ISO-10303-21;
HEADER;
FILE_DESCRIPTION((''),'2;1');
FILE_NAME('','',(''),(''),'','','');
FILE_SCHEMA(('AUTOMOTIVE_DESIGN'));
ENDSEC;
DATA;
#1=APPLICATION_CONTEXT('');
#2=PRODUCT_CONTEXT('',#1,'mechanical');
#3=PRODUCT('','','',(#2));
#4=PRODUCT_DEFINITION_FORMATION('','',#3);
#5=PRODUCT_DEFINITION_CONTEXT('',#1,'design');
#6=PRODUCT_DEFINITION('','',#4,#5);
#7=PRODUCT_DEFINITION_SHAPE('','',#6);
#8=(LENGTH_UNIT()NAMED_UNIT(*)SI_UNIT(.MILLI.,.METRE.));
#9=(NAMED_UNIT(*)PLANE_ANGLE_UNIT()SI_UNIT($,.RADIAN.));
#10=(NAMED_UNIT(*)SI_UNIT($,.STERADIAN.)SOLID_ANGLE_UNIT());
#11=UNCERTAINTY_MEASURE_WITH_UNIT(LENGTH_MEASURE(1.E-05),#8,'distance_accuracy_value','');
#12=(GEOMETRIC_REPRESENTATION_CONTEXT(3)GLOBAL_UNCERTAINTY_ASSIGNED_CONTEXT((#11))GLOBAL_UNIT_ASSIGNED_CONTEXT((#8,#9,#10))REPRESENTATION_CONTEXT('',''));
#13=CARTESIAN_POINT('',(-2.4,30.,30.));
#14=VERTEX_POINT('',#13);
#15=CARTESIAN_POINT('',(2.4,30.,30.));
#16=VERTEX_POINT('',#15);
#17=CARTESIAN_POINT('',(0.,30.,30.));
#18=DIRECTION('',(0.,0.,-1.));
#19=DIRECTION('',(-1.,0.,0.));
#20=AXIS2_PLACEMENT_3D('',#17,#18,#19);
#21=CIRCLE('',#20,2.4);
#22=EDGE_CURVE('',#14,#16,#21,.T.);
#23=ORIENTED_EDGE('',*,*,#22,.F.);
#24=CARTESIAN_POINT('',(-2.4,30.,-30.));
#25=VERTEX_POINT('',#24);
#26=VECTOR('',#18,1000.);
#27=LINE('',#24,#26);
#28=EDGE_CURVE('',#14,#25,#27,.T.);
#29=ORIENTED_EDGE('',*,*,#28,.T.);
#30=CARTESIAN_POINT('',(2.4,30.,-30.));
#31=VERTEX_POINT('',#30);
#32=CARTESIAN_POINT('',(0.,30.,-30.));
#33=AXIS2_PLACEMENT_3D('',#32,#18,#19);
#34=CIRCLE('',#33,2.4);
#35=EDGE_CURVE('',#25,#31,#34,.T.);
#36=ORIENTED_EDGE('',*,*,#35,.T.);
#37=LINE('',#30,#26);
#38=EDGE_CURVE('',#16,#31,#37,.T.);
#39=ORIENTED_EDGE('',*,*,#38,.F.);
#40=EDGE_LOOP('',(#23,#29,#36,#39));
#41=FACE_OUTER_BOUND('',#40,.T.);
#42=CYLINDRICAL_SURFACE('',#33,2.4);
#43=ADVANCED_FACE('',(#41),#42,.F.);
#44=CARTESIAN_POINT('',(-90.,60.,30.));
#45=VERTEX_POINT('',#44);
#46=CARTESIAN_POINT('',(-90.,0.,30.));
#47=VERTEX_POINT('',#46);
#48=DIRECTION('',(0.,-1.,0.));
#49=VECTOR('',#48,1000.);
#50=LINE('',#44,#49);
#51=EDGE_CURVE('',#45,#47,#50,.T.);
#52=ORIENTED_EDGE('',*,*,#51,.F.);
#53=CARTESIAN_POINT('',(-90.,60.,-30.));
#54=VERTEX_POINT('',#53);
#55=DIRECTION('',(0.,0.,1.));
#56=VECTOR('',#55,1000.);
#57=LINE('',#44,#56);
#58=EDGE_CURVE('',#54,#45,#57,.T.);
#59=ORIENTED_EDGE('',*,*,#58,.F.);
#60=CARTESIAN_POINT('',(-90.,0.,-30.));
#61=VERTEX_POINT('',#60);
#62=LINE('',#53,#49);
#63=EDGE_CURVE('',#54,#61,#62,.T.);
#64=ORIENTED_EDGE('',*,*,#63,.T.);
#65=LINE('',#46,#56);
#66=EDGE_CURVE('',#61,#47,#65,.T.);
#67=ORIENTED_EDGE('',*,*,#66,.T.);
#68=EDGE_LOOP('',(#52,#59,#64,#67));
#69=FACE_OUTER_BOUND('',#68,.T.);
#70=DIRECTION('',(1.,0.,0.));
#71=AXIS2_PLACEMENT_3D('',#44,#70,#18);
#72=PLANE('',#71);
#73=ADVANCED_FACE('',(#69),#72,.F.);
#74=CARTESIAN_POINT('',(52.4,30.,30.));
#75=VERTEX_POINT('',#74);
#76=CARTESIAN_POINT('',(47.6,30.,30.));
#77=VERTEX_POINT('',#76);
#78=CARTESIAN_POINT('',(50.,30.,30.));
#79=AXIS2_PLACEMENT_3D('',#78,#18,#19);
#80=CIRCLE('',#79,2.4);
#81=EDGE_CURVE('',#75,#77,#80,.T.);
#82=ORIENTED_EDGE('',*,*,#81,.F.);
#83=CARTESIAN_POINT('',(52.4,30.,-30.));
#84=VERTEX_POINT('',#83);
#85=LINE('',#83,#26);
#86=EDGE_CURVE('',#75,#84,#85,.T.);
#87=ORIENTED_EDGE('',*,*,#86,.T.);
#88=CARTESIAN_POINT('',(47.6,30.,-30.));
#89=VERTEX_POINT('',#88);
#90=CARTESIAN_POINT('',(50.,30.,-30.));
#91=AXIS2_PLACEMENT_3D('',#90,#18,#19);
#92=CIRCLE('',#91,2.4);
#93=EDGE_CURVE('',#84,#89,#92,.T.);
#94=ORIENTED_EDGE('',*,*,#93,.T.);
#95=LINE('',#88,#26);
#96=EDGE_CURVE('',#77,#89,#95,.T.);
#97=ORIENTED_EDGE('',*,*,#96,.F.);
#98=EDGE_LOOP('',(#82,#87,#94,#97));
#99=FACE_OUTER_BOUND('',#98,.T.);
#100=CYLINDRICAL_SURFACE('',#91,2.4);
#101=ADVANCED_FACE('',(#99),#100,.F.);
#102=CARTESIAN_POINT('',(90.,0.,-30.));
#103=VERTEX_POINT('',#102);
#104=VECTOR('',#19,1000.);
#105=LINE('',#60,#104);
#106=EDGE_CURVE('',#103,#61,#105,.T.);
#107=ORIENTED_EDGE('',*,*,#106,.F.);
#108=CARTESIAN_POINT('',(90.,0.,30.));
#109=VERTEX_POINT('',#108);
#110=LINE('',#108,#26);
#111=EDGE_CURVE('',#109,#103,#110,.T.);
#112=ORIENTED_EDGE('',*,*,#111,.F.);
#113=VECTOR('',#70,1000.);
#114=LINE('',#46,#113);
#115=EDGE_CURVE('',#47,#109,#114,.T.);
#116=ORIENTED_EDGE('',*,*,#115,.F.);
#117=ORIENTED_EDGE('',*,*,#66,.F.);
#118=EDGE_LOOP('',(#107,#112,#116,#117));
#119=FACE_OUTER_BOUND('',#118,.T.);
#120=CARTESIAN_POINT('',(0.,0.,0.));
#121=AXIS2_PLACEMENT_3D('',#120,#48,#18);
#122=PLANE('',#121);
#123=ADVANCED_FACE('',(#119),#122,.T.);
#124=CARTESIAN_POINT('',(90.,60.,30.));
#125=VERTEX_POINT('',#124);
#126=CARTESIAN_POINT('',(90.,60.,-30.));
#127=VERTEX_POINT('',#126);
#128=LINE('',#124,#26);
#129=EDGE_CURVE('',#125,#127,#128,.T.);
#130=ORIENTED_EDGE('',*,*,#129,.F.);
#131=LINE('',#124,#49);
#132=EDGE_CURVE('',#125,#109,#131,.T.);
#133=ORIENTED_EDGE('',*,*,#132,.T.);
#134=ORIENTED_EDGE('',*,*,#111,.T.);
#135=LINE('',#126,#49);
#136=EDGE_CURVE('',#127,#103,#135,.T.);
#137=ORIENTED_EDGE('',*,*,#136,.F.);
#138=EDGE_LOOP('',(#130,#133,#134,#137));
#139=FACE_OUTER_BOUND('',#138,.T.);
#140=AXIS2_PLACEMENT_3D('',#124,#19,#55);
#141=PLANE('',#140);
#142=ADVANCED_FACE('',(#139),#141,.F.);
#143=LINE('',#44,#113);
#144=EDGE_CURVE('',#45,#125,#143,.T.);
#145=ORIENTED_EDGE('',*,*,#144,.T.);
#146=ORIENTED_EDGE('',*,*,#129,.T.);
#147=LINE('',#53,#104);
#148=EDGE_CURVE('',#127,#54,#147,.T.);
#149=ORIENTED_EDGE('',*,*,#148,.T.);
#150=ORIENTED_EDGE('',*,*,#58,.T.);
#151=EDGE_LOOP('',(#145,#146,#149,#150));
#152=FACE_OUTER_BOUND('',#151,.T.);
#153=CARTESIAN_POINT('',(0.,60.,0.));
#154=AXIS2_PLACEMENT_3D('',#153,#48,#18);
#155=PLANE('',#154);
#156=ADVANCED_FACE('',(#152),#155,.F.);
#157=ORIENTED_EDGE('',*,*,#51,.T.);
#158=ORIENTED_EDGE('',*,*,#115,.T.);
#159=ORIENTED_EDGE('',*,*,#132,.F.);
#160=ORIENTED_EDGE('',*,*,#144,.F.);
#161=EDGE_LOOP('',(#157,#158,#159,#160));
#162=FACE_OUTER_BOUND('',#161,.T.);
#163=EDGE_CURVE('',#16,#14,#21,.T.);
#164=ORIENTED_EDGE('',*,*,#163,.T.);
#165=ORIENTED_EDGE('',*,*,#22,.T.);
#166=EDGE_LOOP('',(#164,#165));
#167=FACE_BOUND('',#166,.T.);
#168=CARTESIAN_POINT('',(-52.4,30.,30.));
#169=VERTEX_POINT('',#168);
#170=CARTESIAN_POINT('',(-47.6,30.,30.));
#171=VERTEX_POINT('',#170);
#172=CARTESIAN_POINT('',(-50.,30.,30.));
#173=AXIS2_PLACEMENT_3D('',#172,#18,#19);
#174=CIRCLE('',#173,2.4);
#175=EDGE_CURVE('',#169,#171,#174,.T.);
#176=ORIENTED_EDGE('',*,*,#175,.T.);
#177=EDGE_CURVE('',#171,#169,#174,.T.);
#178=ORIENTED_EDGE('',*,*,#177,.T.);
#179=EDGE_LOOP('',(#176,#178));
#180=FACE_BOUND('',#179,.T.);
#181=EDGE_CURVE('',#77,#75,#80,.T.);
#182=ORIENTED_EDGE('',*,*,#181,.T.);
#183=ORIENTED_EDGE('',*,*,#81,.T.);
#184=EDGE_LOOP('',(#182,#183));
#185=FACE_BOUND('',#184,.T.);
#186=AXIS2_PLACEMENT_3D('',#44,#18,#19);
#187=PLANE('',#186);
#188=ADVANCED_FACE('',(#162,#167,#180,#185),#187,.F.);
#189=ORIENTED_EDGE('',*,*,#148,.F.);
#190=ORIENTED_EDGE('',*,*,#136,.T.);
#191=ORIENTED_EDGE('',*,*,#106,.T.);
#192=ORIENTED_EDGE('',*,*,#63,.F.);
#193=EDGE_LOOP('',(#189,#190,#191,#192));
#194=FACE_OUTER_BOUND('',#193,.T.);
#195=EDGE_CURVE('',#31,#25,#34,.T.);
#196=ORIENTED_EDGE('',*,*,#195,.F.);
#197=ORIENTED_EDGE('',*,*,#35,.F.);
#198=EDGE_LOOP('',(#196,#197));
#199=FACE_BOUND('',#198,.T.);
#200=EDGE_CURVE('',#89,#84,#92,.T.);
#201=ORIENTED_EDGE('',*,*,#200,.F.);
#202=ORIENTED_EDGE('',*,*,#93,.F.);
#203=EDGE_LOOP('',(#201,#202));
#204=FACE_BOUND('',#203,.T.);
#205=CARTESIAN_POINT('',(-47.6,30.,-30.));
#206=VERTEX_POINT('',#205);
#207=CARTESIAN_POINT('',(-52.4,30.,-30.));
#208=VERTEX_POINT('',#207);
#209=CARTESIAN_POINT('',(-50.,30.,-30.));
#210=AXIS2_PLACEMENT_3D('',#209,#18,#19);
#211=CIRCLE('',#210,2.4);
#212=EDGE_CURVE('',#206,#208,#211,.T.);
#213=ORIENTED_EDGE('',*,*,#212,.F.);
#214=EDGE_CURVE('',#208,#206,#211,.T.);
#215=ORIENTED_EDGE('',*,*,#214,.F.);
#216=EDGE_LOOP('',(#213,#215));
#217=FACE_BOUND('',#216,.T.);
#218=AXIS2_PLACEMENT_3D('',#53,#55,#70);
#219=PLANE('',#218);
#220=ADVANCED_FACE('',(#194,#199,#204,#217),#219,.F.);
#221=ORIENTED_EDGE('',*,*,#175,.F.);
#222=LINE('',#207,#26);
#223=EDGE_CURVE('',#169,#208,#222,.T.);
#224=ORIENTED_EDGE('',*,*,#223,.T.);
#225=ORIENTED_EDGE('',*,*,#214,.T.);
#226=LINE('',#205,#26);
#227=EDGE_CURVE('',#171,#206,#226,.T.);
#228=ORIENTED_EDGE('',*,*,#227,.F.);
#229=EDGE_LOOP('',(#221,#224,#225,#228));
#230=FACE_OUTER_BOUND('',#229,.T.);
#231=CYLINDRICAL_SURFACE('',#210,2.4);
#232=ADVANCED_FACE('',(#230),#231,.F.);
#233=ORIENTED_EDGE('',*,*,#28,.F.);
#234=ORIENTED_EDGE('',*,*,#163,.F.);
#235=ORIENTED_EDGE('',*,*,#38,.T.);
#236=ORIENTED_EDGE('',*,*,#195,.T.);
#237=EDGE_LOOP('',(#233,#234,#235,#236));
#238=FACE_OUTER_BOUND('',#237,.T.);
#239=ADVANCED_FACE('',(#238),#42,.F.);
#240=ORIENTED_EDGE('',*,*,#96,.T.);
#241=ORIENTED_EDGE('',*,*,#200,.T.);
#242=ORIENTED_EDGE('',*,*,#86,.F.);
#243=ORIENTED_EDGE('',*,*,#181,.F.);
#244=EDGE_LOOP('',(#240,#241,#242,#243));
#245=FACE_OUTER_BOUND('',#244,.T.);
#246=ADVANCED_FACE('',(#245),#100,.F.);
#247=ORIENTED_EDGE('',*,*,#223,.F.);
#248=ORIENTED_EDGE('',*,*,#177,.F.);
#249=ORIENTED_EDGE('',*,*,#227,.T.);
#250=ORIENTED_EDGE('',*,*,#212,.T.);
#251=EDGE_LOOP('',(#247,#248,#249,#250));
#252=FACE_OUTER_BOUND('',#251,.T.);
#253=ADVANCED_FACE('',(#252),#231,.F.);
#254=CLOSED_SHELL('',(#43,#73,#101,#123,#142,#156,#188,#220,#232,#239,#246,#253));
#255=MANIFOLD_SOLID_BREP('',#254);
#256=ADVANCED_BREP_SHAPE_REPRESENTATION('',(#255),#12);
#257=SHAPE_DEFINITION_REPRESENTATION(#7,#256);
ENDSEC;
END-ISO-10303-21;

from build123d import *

# Parameters (mm, degrees)
SKETCH_1_W         = 180
SKETCH_1_H         = 60
EXTRUDE_1_DEPTH    = 60
HOLE_WIZARD_M4_1_D = 4.8


with BuildPart() as part:
    # 草图1 → 凸台-拉伸1 (new body)
    with BuildSketch(Plane(origin=(0, 0, 0), x_dir=(1, 0, 0), z_dir=(0, 1, 0))):
        Rectangle(SKETCH_1_W, SKETCH_1_H)
    extrude(amount=EXTRUDE_1_DEPTH)

    # M4 间隙孔1 (through all)
    with Locations(Plane(origin=(0, 0, -30), x_dir=(-1, 0, 0), z_dir=(0, 0, -1))):
        with Locations((0, 30), (50, 30), (-50, 30)):
            Hole(HOLE_WIZARD_M4_1_D / 2)


solid = part.part
